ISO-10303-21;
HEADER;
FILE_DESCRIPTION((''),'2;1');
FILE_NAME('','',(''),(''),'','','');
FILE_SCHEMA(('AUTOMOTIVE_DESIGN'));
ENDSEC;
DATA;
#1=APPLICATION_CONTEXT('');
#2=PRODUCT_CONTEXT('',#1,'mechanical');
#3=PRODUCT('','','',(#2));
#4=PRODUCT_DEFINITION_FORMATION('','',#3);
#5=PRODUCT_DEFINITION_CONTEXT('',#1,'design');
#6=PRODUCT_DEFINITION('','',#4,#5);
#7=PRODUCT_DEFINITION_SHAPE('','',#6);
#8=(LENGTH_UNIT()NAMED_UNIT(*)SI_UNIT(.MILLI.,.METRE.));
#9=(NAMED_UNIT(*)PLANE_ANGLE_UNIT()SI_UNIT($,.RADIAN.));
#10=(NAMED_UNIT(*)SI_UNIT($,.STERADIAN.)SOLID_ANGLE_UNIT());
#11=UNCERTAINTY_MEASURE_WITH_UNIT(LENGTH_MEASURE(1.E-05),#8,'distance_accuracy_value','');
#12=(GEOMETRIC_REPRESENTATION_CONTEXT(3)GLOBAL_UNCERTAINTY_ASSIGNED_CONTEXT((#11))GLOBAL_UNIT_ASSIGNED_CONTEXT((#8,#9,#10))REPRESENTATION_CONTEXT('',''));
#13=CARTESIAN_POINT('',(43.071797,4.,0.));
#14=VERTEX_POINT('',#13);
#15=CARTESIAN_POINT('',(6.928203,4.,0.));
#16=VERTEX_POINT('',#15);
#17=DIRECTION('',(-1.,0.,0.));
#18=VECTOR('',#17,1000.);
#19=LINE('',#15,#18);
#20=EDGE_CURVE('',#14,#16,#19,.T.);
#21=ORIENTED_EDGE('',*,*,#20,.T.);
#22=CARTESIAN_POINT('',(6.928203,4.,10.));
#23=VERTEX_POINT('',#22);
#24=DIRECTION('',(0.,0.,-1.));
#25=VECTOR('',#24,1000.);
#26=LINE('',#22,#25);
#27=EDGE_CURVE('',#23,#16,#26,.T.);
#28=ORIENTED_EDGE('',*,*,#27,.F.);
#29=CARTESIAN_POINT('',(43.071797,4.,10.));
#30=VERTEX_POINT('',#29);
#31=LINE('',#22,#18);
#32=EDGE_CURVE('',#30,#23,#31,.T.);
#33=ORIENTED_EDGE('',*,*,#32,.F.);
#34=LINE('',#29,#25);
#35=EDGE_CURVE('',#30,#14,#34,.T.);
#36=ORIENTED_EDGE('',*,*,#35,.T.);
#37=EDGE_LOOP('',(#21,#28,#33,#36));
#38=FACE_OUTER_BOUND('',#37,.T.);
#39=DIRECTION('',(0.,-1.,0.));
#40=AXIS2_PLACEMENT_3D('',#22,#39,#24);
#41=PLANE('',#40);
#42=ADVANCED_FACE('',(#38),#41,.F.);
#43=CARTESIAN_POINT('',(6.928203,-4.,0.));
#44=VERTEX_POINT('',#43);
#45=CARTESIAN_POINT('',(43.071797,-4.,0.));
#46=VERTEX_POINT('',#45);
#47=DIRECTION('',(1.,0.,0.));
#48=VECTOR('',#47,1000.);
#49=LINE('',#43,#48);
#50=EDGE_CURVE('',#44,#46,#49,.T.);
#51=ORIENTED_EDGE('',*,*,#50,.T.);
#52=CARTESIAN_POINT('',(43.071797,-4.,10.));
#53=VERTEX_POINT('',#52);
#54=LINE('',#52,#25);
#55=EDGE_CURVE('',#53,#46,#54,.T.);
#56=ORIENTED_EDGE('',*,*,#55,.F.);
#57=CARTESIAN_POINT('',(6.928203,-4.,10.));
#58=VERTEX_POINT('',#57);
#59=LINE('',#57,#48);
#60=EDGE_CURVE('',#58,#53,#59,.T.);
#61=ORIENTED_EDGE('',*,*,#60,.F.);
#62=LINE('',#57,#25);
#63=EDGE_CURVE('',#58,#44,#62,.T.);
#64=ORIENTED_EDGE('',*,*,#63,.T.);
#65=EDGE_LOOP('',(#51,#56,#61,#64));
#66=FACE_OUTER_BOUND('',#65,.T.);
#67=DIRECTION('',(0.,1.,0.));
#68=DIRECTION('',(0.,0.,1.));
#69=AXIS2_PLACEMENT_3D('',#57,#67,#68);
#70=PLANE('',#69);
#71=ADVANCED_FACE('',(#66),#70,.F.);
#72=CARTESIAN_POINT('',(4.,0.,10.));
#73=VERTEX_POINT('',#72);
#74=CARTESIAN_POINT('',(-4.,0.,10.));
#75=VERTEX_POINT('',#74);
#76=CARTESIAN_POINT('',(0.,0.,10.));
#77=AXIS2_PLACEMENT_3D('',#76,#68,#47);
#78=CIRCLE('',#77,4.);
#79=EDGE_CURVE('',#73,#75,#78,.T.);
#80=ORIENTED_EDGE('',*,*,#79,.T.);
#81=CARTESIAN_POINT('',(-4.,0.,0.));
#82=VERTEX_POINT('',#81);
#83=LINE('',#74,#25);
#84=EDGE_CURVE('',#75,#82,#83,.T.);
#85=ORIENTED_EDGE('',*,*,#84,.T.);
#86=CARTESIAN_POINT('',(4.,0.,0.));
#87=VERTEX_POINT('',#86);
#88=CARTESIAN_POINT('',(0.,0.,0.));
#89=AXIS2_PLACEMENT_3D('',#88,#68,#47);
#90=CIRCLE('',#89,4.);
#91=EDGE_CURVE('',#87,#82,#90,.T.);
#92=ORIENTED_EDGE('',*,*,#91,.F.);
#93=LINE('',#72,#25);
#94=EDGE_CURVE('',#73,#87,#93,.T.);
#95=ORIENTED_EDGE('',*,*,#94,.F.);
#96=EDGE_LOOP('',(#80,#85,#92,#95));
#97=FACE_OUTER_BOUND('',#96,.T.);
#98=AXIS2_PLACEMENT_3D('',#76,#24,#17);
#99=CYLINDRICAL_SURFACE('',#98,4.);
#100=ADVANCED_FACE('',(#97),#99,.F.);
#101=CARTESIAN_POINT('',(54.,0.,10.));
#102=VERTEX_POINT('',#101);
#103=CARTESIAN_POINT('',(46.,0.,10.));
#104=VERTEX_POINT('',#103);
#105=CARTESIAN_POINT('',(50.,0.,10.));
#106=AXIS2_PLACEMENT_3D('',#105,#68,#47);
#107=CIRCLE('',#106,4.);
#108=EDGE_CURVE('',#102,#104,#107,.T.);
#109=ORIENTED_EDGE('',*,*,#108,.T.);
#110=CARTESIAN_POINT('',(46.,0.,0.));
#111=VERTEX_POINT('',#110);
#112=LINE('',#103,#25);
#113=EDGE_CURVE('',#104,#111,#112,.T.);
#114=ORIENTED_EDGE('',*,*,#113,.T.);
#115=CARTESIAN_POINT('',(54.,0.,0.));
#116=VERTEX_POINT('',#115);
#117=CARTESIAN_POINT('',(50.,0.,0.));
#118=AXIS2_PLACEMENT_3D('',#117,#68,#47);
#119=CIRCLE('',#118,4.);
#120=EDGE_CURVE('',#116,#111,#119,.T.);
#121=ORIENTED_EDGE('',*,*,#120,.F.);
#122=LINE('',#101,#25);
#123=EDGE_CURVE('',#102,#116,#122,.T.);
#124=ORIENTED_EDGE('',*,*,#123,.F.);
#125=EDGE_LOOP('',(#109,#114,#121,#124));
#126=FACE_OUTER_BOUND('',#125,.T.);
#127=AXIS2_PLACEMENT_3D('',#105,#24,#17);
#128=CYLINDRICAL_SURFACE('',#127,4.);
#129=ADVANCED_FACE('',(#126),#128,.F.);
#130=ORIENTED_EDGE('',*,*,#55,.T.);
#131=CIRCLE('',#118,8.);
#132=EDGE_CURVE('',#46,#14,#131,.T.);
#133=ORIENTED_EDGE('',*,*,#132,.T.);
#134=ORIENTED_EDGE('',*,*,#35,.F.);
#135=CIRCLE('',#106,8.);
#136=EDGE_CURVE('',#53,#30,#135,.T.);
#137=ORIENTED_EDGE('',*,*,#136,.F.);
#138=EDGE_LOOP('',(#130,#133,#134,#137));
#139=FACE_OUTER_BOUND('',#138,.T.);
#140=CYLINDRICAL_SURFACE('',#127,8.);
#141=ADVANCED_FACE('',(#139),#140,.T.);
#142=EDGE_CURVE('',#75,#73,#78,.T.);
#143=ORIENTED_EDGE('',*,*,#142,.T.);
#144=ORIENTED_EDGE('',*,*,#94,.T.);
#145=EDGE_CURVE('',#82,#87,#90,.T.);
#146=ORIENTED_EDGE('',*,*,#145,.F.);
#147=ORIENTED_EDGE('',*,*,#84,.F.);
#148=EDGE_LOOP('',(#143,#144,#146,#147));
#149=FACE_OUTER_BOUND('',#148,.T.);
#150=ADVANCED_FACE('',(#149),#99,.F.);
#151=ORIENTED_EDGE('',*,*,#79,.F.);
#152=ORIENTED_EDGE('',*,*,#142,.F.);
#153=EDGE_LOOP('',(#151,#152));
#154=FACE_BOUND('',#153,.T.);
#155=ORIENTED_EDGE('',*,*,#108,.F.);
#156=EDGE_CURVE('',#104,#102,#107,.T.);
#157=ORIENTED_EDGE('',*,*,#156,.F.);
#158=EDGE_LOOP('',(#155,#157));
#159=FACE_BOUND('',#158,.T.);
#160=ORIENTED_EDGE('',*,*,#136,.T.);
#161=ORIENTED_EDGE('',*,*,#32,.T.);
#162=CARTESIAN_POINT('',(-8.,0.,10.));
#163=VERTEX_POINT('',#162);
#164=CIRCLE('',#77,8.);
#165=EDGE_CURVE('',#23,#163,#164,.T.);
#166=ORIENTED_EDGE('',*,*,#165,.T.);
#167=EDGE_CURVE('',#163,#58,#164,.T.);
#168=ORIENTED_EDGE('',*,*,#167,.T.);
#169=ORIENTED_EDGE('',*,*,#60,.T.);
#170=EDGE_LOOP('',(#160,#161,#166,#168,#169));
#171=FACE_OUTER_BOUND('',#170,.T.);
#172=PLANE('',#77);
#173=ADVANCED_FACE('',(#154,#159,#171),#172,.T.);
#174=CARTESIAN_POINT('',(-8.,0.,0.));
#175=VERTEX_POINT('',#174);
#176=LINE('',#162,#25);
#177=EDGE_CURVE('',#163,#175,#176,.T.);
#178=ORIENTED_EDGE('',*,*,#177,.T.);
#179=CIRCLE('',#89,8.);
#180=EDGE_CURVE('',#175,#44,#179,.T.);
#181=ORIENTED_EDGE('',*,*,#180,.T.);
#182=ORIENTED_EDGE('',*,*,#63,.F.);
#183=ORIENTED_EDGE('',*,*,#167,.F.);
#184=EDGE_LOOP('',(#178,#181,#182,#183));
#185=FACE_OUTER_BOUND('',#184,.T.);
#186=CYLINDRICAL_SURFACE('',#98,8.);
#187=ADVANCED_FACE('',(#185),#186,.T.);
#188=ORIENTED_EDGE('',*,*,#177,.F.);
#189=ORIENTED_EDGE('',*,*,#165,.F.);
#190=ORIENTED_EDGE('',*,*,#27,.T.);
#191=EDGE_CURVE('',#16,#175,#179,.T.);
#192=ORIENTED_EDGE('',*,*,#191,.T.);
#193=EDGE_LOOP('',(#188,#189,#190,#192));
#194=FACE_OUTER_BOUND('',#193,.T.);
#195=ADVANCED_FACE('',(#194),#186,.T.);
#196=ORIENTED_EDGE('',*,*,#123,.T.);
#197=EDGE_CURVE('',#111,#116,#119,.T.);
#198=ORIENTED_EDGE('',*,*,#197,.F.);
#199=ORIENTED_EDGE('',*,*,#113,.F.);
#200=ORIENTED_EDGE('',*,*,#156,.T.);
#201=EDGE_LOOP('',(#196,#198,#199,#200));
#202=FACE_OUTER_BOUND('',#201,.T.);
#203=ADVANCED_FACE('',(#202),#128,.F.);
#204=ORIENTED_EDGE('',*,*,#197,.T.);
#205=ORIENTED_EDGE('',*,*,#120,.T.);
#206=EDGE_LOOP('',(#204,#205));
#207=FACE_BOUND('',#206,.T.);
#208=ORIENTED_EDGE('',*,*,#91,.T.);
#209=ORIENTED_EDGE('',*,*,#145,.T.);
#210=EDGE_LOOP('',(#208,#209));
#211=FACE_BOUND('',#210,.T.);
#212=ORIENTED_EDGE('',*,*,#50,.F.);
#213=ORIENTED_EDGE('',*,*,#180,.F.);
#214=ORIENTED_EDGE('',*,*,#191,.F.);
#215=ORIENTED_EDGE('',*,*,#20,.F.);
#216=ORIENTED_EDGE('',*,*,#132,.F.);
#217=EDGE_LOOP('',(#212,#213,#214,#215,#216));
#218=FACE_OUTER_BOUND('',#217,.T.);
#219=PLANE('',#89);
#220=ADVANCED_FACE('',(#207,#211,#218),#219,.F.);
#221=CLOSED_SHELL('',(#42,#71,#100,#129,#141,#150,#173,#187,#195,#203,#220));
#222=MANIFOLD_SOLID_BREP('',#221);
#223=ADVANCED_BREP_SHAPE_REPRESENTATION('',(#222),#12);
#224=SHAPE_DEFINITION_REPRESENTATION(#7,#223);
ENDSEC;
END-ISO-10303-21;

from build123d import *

# Parameters (mm, degrees)
SKETCH1_R           = 4
BOSS_EXTRUDE1_DEPTH = 10


with BuildPart() as part:
    # Sketch1 → Boss-Extrude1 (new body)
    with BuildSketch(Plane.XY):
        with BuildLine():
            Line((6.92820323, -4), (43.07179677, -4))
            ThreePointArc((43.07179677, -4), (58, 0), (43.07179677, 4))
            Line((43.07179677, 4), (6.92820323, 4))
            ThreePointArc((6.92820323, 4), (-8, 0), (6.92820323, -4))
        make_face()
        Circle(SKETCH1_R, mode=Mode.SUBTRACT)
        with Locations((50, 0)):
            Circle(SKETCH1_R, mode=Mode.SUBTRACT)
    extrude(amount=BOSS_EXTRUDE1_DEPTH)


solid = part.part
